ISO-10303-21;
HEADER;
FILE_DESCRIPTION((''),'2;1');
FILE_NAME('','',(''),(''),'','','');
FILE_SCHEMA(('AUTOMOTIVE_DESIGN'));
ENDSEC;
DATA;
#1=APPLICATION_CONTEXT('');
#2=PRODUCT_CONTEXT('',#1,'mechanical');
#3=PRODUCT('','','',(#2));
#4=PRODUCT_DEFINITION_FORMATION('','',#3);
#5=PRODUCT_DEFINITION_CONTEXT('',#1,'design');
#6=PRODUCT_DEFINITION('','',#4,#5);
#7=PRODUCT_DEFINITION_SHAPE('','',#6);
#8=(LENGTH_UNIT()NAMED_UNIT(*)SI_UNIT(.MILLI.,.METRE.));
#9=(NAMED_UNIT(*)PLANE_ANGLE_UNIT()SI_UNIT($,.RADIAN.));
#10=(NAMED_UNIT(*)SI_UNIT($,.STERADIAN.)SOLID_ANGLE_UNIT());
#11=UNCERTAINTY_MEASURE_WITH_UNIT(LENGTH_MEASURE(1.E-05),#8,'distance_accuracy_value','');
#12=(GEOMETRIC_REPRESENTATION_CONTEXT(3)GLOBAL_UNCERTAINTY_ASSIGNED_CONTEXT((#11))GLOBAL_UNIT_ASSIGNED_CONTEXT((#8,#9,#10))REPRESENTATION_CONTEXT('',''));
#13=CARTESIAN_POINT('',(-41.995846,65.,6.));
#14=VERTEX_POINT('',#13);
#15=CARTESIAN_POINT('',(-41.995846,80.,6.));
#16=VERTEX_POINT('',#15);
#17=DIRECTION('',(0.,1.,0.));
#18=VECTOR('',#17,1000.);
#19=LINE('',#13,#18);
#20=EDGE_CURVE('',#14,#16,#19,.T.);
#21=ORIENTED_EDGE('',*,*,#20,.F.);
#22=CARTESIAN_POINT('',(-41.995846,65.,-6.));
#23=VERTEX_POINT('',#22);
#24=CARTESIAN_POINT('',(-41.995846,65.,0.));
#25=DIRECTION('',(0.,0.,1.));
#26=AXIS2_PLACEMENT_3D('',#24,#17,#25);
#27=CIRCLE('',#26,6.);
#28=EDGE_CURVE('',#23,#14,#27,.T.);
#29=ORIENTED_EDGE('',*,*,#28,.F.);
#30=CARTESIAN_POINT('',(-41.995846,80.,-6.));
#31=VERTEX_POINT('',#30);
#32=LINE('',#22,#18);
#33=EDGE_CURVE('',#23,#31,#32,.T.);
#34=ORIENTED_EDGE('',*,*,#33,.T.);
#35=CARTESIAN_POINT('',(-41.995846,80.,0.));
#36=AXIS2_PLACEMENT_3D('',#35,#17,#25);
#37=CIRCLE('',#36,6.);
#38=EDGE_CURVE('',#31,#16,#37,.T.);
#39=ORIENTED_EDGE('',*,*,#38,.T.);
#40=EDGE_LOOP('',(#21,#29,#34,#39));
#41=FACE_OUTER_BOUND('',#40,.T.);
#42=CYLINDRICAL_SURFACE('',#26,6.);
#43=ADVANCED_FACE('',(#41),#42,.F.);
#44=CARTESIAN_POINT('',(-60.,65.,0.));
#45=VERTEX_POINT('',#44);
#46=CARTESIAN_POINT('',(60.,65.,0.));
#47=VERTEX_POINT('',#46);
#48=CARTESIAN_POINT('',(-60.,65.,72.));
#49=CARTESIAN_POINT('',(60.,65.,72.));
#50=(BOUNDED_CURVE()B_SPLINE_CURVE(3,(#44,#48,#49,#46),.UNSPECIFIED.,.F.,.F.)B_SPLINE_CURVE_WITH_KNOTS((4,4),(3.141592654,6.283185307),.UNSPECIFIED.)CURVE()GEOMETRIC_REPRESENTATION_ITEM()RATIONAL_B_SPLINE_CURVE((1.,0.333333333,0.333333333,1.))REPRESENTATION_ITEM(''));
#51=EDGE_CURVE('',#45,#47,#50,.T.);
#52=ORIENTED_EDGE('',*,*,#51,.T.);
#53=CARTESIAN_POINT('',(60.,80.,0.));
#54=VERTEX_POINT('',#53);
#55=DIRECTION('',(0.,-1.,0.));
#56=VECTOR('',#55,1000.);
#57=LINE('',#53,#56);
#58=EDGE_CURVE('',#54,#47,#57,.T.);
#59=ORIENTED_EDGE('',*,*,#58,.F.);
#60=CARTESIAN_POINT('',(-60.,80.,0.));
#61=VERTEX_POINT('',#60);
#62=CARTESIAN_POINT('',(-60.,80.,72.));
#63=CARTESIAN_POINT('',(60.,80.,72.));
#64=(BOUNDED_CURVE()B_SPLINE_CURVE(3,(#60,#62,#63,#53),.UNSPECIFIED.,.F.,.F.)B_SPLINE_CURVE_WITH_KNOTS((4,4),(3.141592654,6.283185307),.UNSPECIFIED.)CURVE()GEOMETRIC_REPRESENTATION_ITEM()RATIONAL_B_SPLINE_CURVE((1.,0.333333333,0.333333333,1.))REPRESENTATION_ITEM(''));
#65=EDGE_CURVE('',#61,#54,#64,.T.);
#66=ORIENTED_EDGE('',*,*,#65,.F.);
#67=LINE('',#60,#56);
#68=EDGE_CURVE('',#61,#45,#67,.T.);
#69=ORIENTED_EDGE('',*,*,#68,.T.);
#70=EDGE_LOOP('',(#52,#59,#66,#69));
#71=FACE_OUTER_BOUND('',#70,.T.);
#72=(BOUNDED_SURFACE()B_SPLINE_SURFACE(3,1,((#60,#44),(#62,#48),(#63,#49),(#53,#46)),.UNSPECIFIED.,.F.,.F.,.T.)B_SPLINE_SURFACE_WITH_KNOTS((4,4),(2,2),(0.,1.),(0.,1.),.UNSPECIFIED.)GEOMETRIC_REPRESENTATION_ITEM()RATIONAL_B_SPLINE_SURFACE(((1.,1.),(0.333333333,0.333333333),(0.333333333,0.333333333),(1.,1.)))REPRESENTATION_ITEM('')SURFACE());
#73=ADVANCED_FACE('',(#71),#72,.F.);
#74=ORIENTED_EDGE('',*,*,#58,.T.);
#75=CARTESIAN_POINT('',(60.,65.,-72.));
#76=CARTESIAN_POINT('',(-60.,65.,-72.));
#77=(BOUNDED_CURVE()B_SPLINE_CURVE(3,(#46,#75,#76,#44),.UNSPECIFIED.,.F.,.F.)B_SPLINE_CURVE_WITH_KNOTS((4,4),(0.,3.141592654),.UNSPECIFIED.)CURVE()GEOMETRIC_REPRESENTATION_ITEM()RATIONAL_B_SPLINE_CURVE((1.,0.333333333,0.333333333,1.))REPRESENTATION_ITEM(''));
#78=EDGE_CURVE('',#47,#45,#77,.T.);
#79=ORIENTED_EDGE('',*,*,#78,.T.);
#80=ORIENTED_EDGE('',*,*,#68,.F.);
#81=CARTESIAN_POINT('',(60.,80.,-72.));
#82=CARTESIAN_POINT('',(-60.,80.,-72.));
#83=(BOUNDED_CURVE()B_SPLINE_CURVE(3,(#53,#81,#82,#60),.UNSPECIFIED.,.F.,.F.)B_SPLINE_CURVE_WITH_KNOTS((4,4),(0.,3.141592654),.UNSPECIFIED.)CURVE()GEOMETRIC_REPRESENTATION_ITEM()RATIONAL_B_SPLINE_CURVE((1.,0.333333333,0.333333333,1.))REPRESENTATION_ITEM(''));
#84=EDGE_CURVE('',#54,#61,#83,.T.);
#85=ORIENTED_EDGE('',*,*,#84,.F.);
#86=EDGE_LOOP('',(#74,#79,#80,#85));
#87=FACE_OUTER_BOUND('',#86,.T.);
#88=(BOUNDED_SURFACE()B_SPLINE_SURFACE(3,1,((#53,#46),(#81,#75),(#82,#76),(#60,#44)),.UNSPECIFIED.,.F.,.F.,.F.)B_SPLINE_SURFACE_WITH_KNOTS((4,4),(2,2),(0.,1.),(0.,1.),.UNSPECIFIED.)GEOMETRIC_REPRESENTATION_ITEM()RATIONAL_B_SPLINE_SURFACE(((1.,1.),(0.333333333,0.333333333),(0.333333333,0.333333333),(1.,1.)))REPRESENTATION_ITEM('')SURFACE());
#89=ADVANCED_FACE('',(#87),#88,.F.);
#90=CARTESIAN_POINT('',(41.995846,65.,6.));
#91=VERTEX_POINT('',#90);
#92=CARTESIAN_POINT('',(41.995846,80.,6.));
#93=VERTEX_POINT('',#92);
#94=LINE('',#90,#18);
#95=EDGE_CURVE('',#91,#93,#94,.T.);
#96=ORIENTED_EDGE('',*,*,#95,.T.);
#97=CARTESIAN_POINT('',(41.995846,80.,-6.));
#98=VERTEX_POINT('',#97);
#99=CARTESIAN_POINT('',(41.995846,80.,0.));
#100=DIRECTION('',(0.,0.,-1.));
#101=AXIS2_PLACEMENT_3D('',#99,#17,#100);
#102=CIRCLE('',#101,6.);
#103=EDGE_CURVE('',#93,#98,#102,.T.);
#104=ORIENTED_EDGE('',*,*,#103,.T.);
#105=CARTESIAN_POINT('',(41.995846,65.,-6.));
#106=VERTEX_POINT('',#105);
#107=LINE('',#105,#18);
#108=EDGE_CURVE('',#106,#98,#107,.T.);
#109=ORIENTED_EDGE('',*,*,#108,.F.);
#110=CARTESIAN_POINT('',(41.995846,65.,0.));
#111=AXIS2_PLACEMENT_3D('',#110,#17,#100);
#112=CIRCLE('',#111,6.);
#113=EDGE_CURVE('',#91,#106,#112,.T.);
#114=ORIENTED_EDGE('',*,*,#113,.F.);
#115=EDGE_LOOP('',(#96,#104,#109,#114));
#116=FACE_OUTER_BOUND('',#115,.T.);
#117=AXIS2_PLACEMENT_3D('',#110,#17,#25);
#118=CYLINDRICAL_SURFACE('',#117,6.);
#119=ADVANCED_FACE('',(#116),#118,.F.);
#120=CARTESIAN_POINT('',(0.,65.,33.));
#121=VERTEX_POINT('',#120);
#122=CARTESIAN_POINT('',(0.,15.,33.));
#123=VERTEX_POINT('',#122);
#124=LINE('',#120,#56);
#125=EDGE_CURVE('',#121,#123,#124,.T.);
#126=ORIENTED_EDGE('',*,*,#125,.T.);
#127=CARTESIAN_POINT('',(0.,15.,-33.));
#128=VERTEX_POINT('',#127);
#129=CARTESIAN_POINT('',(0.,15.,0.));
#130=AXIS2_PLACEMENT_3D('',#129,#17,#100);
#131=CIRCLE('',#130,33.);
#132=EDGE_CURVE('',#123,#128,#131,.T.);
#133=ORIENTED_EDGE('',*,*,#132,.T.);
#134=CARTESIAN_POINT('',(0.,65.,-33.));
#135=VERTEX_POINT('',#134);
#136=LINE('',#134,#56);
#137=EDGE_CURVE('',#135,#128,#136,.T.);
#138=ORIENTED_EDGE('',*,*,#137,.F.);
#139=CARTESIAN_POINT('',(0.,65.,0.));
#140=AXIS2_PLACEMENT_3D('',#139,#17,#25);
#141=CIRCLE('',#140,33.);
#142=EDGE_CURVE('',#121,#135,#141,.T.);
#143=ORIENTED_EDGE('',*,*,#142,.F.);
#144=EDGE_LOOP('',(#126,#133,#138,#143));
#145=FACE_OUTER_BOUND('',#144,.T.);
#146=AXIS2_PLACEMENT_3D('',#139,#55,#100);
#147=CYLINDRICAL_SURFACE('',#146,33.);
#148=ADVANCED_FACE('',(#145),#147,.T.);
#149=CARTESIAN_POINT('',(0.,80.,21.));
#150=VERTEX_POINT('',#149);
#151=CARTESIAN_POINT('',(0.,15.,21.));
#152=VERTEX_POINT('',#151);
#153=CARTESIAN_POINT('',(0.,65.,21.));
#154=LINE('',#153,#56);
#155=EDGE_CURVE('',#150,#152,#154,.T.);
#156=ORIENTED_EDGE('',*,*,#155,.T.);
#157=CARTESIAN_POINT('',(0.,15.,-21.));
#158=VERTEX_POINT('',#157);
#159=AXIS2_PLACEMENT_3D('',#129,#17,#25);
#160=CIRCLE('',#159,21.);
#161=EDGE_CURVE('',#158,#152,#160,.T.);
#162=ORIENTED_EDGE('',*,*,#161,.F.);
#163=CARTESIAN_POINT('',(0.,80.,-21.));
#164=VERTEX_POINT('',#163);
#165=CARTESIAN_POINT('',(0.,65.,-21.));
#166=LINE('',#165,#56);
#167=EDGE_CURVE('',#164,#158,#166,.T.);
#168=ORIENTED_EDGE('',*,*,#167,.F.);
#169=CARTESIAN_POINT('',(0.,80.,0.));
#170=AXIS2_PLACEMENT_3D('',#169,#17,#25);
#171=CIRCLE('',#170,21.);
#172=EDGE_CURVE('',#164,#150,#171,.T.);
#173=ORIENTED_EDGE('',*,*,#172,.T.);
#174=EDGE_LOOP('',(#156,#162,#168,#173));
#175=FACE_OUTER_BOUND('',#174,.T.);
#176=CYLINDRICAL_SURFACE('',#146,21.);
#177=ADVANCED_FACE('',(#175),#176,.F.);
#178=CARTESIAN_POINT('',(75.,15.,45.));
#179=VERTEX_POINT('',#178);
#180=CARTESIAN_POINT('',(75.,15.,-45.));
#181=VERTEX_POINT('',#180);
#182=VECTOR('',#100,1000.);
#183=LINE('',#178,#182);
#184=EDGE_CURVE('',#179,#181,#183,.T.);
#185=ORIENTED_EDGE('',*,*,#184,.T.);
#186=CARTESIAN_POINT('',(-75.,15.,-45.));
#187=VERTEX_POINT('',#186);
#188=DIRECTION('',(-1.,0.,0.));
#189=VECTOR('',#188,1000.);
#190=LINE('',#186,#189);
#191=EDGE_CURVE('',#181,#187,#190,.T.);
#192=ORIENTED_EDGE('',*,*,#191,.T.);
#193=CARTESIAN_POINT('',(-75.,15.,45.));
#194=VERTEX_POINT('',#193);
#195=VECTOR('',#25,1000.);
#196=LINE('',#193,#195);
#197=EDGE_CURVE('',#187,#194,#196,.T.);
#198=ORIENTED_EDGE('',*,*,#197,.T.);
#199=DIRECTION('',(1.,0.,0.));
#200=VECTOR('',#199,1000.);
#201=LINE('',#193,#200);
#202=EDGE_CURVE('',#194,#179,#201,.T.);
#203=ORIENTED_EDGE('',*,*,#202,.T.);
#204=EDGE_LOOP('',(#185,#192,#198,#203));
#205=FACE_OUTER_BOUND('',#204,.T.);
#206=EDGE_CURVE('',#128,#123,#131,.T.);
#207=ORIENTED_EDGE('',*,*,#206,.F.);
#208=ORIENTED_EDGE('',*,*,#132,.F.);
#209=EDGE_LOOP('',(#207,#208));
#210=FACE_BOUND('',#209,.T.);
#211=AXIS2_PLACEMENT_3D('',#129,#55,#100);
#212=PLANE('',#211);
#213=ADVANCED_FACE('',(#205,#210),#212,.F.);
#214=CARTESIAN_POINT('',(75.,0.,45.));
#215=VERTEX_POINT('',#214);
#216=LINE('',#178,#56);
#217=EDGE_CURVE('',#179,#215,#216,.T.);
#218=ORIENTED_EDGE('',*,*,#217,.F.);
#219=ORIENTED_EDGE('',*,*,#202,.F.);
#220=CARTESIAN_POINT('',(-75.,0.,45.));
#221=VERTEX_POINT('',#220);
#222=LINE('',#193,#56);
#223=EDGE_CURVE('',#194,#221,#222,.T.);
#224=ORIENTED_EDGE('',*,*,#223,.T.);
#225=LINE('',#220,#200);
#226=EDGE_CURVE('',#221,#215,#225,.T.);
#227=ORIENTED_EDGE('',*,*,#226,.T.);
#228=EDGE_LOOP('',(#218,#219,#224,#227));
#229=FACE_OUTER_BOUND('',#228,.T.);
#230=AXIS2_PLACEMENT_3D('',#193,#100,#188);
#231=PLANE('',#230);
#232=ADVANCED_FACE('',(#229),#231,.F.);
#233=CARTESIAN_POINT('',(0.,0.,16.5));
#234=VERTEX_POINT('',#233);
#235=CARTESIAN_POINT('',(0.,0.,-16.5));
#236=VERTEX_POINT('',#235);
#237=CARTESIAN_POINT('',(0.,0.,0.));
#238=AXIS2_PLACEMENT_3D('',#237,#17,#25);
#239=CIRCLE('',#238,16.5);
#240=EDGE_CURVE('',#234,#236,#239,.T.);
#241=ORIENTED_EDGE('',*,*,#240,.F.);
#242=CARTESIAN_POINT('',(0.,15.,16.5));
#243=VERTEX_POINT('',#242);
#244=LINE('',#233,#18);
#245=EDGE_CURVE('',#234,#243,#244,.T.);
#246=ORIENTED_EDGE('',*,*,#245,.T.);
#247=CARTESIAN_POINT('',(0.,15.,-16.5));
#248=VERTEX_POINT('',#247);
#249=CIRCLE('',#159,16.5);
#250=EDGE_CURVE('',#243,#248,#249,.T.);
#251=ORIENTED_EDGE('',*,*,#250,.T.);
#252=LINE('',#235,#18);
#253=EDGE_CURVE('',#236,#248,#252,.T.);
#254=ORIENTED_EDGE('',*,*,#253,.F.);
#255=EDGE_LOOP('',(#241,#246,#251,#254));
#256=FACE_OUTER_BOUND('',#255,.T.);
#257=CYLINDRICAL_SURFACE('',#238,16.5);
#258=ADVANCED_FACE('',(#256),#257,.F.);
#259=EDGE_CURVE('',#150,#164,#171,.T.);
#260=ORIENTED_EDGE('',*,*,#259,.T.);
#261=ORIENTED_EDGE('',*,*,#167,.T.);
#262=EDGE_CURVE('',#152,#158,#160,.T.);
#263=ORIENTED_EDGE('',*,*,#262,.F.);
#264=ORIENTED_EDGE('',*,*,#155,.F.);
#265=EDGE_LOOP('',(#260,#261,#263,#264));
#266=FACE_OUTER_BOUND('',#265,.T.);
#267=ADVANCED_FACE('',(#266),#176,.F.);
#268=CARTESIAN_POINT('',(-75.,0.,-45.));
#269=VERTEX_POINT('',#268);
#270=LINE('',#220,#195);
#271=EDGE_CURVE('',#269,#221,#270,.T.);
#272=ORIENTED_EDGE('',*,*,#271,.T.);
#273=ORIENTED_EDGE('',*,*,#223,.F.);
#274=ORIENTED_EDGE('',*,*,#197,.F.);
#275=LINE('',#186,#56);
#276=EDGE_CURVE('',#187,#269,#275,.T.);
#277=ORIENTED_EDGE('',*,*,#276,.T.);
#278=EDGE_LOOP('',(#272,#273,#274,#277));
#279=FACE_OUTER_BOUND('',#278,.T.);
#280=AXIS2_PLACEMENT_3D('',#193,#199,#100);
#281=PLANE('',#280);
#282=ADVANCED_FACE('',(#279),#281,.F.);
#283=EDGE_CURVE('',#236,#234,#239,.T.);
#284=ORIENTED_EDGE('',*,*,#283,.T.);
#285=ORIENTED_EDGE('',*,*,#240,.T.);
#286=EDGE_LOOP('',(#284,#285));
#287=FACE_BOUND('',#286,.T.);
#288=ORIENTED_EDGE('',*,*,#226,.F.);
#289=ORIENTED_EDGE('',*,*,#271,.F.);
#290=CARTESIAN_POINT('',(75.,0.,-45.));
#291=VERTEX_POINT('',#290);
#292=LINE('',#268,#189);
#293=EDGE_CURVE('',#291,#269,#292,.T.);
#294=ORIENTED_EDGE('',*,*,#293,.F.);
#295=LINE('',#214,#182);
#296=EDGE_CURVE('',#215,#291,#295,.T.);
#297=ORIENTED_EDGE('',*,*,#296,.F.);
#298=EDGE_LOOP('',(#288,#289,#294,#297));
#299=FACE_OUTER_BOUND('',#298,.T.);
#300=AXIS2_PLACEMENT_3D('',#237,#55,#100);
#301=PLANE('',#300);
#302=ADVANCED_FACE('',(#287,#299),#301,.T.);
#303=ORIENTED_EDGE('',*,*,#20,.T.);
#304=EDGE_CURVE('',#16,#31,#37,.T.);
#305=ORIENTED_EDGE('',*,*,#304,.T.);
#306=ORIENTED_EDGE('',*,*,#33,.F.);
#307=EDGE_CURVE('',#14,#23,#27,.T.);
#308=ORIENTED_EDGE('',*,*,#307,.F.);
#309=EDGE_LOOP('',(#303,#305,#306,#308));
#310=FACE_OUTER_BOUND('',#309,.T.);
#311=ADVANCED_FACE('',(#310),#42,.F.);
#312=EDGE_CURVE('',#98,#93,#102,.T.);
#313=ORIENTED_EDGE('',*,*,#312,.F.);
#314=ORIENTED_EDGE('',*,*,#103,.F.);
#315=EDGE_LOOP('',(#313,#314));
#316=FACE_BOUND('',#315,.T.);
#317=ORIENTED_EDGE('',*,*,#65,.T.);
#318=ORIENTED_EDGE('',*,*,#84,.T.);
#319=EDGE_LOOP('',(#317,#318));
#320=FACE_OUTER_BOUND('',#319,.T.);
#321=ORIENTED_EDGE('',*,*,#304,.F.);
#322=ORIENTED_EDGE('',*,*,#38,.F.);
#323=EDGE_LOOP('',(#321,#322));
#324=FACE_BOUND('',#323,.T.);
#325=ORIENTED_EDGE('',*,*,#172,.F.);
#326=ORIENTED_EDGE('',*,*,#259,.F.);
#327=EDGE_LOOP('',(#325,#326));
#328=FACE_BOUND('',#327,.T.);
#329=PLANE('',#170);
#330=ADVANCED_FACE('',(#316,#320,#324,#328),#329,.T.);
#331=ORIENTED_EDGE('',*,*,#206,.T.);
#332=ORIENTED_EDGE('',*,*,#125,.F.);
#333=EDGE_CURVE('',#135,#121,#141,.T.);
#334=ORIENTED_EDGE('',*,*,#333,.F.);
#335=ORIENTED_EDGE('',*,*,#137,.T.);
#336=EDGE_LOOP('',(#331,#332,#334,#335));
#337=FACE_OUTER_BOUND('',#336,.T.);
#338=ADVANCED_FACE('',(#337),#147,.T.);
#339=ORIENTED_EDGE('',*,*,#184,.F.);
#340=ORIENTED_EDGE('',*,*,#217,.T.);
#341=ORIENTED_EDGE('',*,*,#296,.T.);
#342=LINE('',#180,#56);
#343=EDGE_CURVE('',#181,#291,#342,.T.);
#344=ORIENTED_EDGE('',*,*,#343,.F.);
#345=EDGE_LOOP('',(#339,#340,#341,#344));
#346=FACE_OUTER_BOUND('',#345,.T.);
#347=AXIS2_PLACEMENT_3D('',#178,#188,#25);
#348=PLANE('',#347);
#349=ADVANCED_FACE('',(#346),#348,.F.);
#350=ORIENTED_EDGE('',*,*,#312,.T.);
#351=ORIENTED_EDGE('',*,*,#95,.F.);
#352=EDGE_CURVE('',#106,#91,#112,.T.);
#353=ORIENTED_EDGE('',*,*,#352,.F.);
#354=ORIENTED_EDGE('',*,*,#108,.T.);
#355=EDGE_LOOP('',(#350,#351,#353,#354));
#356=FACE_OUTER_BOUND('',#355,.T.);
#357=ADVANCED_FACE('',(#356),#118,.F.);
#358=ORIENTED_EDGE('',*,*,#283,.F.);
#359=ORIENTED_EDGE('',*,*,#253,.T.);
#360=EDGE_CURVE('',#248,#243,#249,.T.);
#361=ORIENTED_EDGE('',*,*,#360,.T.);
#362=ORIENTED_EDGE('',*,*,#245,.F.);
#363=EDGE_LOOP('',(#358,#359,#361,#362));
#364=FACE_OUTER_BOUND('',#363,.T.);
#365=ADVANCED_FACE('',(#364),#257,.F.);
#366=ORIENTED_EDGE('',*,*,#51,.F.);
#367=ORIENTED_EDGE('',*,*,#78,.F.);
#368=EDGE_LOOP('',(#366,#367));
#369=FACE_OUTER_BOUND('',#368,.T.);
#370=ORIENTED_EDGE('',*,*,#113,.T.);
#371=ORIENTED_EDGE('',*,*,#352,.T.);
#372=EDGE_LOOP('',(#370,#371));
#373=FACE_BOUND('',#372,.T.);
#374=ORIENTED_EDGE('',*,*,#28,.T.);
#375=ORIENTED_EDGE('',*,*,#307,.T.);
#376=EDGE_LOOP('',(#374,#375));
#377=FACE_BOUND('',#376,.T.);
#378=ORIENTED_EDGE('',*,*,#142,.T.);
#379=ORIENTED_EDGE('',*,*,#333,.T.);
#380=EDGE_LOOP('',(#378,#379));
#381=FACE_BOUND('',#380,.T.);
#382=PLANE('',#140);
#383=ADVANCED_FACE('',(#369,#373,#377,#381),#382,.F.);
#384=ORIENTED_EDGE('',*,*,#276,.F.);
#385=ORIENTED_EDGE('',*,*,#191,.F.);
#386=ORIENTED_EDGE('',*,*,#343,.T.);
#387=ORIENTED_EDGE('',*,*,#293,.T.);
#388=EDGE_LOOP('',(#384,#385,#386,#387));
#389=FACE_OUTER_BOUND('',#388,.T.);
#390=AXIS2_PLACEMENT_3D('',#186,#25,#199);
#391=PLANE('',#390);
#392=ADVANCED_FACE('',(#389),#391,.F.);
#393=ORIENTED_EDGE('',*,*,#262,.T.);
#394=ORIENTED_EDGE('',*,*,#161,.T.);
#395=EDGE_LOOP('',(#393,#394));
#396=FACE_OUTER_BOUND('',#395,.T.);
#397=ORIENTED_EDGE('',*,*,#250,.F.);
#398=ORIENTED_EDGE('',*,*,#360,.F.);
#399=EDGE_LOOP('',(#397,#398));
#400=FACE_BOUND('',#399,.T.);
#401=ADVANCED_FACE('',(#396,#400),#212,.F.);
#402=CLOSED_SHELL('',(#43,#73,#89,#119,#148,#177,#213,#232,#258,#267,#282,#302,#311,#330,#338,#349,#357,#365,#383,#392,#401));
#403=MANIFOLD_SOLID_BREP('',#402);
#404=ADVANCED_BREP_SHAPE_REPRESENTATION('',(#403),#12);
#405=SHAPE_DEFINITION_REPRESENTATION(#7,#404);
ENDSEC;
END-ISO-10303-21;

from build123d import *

# Parameters (mm, degrees)
BASE_PLATE_SKETCH_W        = 150
BASE_PLATE_SKETCH_H        = 90
BASE_PLATE_150X90X15_DEPTH = 15
BOSS_TUBE_SKETCH_R         = 33
BOSS_TUBE_SKETCH_R_2       = 21
BOSS_TUBE_66_DEPTH         = 50
OVAL_FLANGE_SKETCH_RX      = 60
OVAL_FLANGE_SKETCH_RY      = 36
OVAL_FLANGE_SKETCH_R       = 21
OVAL_FLANGE_120X72_DEPTH   = 15
BASE_BORE_SKETCH_R         = 16.5
BASE_BORE_33_DEPTH         = 15
FLANGE_BOLT_HOLE_SKETCH_R  = 6
FLANGE_BOLT_HOLE_DEPTH     = 15


with BuildPart() as part:
    # Base Plate Sketch → Base Plate 150x90x15 (new body)
    with BuildSketch(Plane(origin=(0, 0, 0), x_dir=(1, 0, 0), z_dir=(0, 1, 0))):
        Rectangle(BASE_PLATE_SKETCH_W, BASE_PLATE_SKETCH_H)
    extrude(amount=BASE_PLATE_150X90X15_DEPTH)

    # Boss Tube Sketch → Boss Tube Ø66 (add)
    with BuildSketch(Plane(origin=(0, 15, 0), x_dir=(1, 0, 0), z_dir=(0, 1, 0))):
        with Locations(Location((0, 0, 0), (0, 0, 90))):
            Circle(BOSS_TUBE_SKETCH_R)
        with Locations(Location((0, 0, 0), (0, 0, 270))):
            Circle(BOSS_TUBE_SKETCH_R_2, mode=Mode.SUBTRACT)
    extrude(amount=BOSS_TUBE_66_DEPTH)

    # Oval Flange Sketch → Oval Flange 120x72 (add)
    with BuildSketch(Plane(origin=(0, 65, 0), x_dir=(1, 0, 0), z_dir=(0, 1, 0))):
        with Locations((0, 0)):
            Ellipse(OVAL_FLANGE_SKETCH_RX, OVAL_FLANGE_SKETCH_RY)
        with Locations(Location((0, 0, 0), (0, 0, 270))):
            Circle(OVAL_FLANGE_SKETCH_R, mode=Mode.SUBTRACT)
    extrude(amount=OVAL_FLANGE_120X72_DEPTH)

    # Base Bore Sketch → Base Bore Ø33 (cut)
    with BuildSketch(Plane(origin=(0, 15, 0), x_dir=(1, 0, 0), z_dir=(0, 1, 0))):
        with Locations(Location((0, 0, 0), (0, 0, 270))):
            Circle(BASE_BORE_SKETCH_R)
    extrude(amount=-BASE_BORE_33_DEPTH, mode=Mode.SUBTRACT)

    # Flange Bolt Hole Sketch → Flange Bolt Hole (cut)
    with BuildSketch(Plane(origin=(0, 80, 0), x_dir=(1, 0, 0), z_dir=(0, 1, 0))):
        with Locations(Location((-41.995846121, 0, 0), (0, 0, 270))):
            Circle(FLANGE_BOLT_HOLE_SKETCH_R)
        with Locations(Location((41.995846121, 0, 0), (0, 0, 90))):
            Circle(FLANGE_BOLT_HOLE_SKETCH_R)
    extrude(amount=-FLANGE_BOLT_HOLE_DEPTH, mode=Mode.SUBTRACT)


solid = part.part
